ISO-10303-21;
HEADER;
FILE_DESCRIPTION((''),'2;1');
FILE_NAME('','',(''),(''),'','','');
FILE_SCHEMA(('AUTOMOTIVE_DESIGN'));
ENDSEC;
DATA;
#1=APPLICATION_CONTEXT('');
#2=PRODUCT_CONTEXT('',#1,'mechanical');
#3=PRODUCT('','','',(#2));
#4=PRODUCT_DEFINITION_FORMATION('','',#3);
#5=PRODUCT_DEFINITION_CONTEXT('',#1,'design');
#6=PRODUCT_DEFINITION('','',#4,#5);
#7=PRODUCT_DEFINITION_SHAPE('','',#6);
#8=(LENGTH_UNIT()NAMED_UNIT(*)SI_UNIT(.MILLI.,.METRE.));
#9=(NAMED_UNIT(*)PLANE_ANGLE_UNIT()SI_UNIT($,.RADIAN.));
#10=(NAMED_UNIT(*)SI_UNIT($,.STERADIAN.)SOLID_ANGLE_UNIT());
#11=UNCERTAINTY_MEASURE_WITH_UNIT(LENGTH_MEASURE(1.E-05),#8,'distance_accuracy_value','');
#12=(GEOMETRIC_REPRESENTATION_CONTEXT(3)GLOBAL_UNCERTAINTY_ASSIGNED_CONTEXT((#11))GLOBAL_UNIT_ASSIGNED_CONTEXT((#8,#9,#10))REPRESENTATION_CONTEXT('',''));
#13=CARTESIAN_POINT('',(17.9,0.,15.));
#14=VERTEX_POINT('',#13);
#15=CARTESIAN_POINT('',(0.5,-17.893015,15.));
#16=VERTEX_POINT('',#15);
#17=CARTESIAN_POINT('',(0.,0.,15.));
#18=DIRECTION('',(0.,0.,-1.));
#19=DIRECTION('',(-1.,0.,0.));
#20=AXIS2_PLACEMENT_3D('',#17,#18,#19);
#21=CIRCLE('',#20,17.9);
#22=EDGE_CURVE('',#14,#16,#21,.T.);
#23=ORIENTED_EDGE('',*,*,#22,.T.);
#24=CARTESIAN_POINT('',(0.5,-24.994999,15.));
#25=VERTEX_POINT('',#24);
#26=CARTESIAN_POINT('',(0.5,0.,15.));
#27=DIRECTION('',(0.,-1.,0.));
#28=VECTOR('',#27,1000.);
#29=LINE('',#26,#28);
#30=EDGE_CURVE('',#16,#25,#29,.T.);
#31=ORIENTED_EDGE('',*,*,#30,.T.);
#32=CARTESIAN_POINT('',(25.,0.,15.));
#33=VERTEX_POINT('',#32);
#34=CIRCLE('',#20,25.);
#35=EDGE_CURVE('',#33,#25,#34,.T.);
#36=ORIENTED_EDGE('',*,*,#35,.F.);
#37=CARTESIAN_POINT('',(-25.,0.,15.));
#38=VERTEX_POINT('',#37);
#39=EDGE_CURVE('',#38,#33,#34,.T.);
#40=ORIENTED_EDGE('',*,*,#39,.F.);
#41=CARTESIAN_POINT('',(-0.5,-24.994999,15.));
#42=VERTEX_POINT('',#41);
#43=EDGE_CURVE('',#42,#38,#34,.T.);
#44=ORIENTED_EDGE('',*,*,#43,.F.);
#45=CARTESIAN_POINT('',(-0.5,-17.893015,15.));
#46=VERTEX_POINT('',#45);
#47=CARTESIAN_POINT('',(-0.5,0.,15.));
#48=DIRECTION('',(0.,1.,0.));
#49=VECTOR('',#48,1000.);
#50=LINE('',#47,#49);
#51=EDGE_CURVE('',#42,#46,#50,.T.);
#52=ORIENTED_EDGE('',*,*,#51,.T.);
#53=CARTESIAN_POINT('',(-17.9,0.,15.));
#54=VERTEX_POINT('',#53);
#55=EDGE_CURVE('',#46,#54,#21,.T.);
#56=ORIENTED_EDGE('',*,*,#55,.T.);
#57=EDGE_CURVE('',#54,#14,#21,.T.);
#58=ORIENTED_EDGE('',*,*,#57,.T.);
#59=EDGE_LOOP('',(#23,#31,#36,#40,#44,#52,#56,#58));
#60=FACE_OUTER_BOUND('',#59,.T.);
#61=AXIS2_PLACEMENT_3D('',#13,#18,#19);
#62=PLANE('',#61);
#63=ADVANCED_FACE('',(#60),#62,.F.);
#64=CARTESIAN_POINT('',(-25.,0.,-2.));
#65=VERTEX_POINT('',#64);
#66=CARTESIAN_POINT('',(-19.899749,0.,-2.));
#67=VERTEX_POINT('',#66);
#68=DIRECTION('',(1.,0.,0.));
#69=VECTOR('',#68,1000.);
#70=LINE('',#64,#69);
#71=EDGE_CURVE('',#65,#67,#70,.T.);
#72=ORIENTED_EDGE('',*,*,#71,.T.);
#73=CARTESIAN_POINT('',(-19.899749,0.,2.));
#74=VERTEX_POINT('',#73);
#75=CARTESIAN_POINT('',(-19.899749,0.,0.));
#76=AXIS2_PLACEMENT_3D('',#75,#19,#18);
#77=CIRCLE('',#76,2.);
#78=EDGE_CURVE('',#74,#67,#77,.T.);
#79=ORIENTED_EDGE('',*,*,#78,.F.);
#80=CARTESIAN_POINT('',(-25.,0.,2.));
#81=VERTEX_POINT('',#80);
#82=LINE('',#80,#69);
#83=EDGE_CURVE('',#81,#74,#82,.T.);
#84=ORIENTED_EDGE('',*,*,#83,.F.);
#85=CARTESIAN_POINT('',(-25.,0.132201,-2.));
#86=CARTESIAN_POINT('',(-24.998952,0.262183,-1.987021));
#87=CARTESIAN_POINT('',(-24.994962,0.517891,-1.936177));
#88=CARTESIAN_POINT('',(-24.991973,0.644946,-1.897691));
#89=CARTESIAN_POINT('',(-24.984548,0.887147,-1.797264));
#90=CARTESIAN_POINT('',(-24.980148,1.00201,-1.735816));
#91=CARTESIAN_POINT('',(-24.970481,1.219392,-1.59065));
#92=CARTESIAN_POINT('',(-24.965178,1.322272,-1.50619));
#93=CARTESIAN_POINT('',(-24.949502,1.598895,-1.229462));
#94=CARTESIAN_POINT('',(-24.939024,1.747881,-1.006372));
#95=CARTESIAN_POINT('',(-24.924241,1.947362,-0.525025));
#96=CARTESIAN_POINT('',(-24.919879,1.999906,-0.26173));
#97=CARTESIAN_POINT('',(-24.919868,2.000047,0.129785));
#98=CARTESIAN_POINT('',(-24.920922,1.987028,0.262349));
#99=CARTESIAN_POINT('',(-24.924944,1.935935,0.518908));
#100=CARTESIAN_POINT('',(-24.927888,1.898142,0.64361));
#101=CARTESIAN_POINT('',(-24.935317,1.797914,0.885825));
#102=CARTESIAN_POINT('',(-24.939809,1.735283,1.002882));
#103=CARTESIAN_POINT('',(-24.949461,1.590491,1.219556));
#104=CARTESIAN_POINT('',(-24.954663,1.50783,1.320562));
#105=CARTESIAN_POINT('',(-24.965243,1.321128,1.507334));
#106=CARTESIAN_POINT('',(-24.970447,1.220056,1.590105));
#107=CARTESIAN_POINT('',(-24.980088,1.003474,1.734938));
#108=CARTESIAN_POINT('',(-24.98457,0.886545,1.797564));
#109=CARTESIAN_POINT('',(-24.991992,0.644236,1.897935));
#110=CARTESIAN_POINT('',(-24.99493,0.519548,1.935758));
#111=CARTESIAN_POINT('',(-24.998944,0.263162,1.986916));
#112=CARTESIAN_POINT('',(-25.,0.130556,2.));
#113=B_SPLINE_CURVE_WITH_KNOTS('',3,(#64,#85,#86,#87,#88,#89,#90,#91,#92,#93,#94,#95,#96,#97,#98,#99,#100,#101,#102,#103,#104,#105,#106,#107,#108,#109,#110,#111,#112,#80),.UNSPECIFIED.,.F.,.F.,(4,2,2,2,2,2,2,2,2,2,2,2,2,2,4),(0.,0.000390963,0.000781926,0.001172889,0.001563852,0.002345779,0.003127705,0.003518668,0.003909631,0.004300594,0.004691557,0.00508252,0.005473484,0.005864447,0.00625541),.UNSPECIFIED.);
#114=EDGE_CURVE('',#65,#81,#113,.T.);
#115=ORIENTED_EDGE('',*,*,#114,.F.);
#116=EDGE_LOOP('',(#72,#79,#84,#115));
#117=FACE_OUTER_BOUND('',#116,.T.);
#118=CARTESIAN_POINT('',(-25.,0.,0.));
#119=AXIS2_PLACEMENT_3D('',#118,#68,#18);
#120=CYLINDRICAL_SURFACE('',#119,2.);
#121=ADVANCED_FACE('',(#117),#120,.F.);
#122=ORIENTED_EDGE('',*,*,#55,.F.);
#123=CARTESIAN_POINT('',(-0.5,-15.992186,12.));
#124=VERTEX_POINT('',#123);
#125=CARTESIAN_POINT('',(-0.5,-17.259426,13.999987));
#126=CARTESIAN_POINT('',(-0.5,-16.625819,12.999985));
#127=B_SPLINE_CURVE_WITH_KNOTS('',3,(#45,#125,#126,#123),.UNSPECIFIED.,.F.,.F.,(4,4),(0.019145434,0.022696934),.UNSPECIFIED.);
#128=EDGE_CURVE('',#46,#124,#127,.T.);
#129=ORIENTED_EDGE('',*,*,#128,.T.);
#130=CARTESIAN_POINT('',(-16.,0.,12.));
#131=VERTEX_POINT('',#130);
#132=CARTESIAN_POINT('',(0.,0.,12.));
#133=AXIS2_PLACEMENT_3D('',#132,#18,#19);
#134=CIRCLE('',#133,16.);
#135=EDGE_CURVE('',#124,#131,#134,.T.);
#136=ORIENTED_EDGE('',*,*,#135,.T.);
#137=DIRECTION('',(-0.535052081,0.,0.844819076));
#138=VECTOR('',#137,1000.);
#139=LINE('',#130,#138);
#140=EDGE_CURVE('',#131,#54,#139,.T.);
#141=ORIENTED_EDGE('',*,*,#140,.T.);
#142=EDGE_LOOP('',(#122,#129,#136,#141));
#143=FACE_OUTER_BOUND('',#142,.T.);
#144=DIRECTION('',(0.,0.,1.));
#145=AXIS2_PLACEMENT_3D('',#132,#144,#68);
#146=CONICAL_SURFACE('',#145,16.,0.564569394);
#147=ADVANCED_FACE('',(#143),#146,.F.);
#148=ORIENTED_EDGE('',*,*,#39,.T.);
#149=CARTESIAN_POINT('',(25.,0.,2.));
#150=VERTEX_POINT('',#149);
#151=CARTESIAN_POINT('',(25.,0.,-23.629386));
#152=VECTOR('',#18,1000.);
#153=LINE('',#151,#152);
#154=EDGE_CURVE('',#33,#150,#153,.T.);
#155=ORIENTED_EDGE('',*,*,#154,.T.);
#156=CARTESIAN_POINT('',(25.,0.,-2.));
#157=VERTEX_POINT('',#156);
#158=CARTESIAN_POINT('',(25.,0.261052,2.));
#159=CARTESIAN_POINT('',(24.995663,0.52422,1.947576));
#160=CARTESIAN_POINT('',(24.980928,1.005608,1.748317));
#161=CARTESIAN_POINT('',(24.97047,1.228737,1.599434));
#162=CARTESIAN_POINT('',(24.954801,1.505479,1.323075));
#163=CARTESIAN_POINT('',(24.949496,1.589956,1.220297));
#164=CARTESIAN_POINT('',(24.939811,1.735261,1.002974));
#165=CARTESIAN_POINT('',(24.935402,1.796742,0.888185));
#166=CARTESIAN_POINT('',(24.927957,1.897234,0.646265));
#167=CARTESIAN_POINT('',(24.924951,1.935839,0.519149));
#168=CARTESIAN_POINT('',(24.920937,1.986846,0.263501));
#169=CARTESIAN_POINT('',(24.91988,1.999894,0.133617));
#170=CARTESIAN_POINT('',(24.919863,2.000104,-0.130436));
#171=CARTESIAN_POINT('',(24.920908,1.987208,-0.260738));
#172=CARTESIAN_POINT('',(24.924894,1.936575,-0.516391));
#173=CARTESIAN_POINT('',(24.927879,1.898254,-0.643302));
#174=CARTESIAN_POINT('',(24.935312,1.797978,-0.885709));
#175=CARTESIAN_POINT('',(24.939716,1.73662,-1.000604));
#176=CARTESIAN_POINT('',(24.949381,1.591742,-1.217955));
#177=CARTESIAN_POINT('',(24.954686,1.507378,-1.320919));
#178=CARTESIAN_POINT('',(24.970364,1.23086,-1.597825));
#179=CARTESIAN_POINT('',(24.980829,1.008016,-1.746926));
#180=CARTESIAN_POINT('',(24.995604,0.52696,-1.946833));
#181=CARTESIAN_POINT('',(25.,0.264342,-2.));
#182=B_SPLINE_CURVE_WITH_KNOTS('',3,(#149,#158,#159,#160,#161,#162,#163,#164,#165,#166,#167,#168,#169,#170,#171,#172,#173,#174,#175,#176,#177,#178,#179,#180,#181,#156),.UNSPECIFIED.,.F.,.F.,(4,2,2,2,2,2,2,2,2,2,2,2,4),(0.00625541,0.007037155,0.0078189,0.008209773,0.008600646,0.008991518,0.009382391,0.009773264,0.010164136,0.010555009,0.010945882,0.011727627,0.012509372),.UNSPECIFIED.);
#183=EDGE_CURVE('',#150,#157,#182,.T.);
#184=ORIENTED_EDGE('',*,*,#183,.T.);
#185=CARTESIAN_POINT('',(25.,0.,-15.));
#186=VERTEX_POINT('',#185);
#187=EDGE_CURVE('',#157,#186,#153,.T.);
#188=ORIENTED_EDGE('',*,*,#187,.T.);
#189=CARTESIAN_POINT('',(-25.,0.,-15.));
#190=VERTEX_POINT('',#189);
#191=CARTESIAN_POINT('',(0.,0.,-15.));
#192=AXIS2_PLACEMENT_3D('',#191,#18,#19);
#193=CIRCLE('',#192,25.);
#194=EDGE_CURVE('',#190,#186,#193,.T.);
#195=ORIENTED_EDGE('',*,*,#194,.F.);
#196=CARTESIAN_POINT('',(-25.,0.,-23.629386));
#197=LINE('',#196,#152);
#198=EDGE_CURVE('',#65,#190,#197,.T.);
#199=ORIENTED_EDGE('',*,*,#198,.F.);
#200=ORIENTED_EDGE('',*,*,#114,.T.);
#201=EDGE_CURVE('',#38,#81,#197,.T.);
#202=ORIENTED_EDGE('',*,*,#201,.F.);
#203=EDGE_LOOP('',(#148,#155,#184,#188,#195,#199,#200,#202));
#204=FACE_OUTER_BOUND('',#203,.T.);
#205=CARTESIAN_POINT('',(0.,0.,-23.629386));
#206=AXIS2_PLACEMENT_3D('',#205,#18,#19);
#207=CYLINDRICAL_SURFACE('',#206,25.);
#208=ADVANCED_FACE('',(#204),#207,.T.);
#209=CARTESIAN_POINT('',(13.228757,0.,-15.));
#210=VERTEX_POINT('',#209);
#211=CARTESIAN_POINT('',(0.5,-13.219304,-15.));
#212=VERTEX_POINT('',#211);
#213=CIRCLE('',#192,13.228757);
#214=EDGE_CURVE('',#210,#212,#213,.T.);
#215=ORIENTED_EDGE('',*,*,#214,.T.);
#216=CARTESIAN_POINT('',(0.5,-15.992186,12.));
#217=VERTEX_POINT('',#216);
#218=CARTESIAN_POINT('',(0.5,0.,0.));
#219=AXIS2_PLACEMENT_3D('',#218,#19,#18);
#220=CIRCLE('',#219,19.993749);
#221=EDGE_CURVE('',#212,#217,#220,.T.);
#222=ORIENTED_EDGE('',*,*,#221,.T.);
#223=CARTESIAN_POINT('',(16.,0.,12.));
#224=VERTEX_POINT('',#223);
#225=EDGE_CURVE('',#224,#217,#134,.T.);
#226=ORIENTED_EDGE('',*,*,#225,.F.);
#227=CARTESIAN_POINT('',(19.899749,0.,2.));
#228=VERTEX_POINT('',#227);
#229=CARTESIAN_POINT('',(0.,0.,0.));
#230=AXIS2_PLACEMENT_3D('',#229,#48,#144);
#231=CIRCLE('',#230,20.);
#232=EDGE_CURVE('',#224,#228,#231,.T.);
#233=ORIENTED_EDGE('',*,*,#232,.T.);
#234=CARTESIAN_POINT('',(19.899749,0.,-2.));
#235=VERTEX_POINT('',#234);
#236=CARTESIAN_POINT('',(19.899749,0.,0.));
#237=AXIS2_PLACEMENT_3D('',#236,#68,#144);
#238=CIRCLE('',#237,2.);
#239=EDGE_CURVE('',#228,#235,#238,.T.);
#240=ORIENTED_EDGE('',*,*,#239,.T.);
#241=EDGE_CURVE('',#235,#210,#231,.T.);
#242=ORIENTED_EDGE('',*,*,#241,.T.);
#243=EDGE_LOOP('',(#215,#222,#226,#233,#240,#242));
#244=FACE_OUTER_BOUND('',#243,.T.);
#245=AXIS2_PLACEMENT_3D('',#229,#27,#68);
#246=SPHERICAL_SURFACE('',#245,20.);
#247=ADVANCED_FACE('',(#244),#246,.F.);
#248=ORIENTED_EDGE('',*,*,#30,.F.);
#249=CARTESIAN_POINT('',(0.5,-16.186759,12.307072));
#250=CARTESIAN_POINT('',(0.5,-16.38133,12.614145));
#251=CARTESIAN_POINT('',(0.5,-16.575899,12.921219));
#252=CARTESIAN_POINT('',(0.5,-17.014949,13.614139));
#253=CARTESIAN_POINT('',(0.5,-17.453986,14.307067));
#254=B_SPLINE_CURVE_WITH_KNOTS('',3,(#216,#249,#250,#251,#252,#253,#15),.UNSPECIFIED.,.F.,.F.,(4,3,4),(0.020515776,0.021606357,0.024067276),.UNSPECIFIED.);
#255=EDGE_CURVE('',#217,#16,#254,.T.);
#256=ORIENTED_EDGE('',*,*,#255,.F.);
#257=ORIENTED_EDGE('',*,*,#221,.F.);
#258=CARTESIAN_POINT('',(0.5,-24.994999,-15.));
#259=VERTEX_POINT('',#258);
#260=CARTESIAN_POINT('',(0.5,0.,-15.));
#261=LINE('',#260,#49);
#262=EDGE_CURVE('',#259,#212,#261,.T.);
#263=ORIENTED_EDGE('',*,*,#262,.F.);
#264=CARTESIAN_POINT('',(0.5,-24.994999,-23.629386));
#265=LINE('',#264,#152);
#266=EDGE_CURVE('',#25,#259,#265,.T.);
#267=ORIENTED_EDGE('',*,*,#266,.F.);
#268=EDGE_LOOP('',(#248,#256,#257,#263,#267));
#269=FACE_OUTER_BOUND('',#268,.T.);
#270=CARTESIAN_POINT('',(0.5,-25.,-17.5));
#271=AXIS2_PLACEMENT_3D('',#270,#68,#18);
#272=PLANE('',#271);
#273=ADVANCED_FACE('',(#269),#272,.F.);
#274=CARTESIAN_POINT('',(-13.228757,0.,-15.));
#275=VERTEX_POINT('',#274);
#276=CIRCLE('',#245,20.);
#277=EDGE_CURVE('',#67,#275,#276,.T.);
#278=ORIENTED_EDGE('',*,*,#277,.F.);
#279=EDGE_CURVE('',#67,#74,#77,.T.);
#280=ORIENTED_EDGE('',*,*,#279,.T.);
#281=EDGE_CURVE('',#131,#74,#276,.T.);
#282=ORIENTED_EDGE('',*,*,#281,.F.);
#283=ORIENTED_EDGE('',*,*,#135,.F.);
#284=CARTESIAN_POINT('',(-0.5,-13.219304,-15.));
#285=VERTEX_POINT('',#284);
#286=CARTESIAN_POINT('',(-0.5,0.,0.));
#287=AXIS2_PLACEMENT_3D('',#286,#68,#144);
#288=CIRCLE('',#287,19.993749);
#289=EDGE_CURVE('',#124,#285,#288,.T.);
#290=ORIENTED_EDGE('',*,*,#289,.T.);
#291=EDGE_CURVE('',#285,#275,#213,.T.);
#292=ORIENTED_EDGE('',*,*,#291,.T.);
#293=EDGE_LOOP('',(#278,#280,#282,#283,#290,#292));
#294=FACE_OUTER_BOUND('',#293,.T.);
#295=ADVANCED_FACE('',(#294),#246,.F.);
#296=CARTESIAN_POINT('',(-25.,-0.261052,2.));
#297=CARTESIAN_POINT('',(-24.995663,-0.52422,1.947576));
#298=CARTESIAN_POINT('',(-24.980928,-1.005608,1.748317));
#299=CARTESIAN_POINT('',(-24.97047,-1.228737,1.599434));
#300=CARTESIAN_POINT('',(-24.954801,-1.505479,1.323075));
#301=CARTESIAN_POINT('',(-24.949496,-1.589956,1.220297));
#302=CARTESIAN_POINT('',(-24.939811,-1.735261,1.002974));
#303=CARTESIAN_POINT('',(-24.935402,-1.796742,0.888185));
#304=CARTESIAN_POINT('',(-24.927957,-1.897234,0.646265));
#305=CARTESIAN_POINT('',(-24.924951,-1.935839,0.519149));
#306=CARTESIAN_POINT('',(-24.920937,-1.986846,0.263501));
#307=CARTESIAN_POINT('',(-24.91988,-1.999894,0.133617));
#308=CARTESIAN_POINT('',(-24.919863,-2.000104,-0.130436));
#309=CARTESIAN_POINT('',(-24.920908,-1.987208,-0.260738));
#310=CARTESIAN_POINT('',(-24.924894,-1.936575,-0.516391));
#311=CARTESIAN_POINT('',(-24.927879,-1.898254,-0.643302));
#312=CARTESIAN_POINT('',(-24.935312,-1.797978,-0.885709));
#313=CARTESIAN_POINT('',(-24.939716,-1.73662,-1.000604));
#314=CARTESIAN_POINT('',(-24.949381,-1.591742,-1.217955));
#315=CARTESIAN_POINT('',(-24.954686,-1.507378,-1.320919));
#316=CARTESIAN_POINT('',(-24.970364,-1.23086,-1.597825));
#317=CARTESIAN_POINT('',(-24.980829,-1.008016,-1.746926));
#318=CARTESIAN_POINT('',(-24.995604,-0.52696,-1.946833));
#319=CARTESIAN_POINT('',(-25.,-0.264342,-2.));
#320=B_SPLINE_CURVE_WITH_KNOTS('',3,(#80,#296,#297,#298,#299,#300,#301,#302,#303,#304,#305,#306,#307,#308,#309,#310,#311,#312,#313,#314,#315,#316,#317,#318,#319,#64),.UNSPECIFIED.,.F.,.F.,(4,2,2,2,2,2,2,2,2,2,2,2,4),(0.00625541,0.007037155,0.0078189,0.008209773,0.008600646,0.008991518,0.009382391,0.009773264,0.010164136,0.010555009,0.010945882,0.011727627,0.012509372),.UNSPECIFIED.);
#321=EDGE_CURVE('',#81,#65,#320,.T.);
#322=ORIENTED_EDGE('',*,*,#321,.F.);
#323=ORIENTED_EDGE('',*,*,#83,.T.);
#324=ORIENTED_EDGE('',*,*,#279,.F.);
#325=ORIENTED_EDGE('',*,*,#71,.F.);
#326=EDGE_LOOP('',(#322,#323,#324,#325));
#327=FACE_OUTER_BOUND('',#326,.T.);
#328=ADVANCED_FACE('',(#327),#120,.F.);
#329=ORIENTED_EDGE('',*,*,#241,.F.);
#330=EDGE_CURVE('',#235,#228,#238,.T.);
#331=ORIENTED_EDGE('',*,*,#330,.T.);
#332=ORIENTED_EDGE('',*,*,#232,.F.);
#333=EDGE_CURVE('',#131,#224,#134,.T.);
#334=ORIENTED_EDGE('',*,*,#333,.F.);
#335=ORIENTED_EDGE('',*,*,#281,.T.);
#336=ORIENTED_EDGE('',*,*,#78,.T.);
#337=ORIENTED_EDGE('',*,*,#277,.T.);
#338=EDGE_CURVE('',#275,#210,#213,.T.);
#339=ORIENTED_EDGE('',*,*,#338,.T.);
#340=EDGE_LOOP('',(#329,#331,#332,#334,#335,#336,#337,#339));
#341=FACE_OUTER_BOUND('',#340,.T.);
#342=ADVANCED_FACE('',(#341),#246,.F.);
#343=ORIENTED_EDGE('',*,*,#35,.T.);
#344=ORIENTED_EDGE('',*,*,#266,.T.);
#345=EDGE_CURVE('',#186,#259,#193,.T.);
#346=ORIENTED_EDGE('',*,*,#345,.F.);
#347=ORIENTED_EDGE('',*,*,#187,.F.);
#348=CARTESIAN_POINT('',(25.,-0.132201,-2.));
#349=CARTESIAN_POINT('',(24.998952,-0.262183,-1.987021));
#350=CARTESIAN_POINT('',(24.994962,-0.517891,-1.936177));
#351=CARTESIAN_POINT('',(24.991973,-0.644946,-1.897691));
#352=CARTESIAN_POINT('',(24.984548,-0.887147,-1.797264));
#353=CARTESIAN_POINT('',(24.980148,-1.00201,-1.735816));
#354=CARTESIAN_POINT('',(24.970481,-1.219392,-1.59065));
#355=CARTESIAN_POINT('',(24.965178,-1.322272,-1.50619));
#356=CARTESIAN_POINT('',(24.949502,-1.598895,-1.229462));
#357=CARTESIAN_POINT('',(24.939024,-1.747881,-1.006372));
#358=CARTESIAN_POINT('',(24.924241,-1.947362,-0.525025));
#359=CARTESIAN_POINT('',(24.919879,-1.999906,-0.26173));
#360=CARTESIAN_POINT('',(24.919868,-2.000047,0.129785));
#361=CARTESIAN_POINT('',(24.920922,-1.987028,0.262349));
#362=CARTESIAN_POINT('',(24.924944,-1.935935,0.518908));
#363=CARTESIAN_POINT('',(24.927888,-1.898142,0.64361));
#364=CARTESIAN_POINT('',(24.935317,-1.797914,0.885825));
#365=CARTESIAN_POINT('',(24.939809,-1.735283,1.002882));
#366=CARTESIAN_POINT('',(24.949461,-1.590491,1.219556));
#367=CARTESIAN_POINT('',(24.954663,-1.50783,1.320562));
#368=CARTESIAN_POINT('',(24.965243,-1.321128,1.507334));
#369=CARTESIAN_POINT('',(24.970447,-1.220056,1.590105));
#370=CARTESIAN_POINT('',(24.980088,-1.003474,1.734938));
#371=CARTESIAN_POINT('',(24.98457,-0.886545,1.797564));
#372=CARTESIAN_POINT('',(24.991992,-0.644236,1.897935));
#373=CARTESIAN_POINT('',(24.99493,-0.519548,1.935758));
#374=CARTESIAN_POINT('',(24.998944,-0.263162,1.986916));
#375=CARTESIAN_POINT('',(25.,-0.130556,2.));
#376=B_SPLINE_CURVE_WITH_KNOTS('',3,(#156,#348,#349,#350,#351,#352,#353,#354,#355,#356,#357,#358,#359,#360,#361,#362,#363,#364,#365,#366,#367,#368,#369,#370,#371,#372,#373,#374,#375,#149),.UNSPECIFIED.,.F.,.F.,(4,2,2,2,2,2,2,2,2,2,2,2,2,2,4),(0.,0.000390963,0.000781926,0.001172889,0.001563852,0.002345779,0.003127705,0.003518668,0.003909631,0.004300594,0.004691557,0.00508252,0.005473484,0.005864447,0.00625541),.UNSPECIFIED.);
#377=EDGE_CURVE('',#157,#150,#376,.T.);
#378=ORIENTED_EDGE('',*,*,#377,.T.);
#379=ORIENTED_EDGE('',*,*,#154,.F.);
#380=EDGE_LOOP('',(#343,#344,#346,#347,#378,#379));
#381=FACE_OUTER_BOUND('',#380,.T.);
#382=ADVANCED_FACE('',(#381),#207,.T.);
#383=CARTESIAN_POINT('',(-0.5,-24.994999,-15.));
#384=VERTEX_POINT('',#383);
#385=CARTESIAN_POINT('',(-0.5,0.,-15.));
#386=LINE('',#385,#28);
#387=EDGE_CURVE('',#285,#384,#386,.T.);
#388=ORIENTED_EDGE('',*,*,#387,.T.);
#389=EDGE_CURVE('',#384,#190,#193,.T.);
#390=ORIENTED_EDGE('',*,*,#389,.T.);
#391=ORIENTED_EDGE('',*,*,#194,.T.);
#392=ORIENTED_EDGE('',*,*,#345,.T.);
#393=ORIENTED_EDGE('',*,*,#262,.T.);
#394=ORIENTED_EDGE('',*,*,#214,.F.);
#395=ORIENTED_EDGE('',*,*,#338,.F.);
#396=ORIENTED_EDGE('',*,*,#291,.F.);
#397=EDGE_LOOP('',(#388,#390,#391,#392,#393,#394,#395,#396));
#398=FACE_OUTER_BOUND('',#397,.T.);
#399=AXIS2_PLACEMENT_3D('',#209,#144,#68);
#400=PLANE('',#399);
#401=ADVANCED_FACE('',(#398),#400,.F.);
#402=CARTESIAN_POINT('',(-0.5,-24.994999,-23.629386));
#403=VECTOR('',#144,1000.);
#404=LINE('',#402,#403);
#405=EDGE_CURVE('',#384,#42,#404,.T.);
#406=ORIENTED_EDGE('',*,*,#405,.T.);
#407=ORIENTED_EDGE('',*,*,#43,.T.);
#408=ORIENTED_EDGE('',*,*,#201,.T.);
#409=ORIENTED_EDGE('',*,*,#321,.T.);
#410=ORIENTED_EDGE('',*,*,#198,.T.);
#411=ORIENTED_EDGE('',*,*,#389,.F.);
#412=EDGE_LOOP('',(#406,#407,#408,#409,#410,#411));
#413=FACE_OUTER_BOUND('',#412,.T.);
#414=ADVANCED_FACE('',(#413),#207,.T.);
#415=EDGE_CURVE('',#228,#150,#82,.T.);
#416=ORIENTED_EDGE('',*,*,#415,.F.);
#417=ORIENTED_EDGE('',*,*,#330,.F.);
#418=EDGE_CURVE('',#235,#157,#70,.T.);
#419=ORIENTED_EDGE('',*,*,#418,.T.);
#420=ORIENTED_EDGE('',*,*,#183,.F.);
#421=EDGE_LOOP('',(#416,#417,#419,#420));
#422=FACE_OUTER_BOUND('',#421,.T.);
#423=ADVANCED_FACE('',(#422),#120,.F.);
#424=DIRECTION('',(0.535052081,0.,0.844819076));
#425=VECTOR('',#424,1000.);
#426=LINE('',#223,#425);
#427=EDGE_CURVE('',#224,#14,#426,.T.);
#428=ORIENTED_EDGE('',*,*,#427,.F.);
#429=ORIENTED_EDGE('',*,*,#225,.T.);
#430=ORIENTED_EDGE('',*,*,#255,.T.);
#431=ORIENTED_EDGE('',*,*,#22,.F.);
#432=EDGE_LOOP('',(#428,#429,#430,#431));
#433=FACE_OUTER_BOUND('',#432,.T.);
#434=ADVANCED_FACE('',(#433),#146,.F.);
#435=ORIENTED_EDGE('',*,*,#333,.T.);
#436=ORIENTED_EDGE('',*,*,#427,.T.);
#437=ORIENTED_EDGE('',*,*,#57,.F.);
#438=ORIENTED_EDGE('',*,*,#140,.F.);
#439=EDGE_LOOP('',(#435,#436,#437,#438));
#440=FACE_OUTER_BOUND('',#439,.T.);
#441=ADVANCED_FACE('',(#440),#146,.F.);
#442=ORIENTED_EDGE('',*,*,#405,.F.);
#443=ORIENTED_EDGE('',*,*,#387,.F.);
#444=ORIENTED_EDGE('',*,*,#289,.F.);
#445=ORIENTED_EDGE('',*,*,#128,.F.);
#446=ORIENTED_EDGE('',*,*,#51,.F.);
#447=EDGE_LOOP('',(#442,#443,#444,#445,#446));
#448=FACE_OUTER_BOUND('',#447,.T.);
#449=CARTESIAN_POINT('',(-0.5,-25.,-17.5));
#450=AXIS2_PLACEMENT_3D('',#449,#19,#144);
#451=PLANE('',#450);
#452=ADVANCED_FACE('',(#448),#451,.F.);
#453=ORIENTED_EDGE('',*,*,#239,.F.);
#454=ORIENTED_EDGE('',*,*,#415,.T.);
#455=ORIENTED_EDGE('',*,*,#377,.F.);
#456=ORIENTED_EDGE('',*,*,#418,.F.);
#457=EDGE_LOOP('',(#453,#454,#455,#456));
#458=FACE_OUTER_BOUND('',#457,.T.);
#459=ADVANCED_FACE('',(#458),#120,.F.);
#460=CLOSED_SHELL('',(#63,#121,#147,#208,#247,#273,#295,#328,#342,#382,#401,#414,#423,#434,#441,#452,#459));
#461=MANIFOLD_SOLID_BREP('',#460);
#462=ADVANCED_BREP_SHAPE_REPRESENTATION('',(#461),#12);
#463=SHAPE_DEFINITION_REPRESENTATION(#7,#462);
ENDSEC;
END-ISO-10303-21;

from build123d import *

# Parameters (mm, degrees)
SKETCH2_W               = 1
SKETCH2_H               = 35
CUT_EXTRUDE1_DEPTH      = 39.405728739
CUT_EXTRUDE2_DEPTH      = 39.405728739
CUT_EXTRUDE2_DEPTH_BACK = 39.405728739
SKETCH3_R               = 2


with BuildPart() as part:
    # Sketch1 → Revolve1 (revolve)
    with BuildSketch(Plane(origin=(0, 0, 0), x_dir=(1, 0, 0), z_dir=(0, 1, 0))):
        with BuildLine():
            Line((17.9, -15), (16, -12))
            ThreePointArc((16, -12), (19.895478191, 2.042044945), (13.228756555, 15))
            Line((13.228756555, 15), (25, 15))
            Line((25, 15), (25, -15))
            Line((25, -15), (17.9, -15))
        make_face()
    revolve(axis=Axis((0, 0, -23.629385965), (0, 0, 1)))

    # Sketch2 → Cut-Extrude1 (cut, through all)
    with BuildSketch(Plane(origin=(0, 0, 0), x_dir=(1, 0, 0), z_dir=(0, 1, 0))):
        Rectangle(SKETCH2_W, SKETCH2_H)
    extrude(amount=-CUT_EXTRUDE1_DEPTH, mode=Mode.SUBTRACT)

    # Sketch3 → Cut-Extrude2 (cut, two sides: drawn at the far end of the back side and taken through both)
    with BuildSketch(Plane(origin=(0, 0, 0), x_dir=(0, 0, -1), z_dir=(1, 0, 0)).offset(-CUT_EXTRUDE2_DEPTH_BACK)):
        Circle(SKETCH3_R)
    extrude(amount=CUT_EXTRUDE2_DEPTH + CUT_EXTRUDE2_DEPTH_BACK, mode=Mode.SUBTRACT)


solid = part.part
